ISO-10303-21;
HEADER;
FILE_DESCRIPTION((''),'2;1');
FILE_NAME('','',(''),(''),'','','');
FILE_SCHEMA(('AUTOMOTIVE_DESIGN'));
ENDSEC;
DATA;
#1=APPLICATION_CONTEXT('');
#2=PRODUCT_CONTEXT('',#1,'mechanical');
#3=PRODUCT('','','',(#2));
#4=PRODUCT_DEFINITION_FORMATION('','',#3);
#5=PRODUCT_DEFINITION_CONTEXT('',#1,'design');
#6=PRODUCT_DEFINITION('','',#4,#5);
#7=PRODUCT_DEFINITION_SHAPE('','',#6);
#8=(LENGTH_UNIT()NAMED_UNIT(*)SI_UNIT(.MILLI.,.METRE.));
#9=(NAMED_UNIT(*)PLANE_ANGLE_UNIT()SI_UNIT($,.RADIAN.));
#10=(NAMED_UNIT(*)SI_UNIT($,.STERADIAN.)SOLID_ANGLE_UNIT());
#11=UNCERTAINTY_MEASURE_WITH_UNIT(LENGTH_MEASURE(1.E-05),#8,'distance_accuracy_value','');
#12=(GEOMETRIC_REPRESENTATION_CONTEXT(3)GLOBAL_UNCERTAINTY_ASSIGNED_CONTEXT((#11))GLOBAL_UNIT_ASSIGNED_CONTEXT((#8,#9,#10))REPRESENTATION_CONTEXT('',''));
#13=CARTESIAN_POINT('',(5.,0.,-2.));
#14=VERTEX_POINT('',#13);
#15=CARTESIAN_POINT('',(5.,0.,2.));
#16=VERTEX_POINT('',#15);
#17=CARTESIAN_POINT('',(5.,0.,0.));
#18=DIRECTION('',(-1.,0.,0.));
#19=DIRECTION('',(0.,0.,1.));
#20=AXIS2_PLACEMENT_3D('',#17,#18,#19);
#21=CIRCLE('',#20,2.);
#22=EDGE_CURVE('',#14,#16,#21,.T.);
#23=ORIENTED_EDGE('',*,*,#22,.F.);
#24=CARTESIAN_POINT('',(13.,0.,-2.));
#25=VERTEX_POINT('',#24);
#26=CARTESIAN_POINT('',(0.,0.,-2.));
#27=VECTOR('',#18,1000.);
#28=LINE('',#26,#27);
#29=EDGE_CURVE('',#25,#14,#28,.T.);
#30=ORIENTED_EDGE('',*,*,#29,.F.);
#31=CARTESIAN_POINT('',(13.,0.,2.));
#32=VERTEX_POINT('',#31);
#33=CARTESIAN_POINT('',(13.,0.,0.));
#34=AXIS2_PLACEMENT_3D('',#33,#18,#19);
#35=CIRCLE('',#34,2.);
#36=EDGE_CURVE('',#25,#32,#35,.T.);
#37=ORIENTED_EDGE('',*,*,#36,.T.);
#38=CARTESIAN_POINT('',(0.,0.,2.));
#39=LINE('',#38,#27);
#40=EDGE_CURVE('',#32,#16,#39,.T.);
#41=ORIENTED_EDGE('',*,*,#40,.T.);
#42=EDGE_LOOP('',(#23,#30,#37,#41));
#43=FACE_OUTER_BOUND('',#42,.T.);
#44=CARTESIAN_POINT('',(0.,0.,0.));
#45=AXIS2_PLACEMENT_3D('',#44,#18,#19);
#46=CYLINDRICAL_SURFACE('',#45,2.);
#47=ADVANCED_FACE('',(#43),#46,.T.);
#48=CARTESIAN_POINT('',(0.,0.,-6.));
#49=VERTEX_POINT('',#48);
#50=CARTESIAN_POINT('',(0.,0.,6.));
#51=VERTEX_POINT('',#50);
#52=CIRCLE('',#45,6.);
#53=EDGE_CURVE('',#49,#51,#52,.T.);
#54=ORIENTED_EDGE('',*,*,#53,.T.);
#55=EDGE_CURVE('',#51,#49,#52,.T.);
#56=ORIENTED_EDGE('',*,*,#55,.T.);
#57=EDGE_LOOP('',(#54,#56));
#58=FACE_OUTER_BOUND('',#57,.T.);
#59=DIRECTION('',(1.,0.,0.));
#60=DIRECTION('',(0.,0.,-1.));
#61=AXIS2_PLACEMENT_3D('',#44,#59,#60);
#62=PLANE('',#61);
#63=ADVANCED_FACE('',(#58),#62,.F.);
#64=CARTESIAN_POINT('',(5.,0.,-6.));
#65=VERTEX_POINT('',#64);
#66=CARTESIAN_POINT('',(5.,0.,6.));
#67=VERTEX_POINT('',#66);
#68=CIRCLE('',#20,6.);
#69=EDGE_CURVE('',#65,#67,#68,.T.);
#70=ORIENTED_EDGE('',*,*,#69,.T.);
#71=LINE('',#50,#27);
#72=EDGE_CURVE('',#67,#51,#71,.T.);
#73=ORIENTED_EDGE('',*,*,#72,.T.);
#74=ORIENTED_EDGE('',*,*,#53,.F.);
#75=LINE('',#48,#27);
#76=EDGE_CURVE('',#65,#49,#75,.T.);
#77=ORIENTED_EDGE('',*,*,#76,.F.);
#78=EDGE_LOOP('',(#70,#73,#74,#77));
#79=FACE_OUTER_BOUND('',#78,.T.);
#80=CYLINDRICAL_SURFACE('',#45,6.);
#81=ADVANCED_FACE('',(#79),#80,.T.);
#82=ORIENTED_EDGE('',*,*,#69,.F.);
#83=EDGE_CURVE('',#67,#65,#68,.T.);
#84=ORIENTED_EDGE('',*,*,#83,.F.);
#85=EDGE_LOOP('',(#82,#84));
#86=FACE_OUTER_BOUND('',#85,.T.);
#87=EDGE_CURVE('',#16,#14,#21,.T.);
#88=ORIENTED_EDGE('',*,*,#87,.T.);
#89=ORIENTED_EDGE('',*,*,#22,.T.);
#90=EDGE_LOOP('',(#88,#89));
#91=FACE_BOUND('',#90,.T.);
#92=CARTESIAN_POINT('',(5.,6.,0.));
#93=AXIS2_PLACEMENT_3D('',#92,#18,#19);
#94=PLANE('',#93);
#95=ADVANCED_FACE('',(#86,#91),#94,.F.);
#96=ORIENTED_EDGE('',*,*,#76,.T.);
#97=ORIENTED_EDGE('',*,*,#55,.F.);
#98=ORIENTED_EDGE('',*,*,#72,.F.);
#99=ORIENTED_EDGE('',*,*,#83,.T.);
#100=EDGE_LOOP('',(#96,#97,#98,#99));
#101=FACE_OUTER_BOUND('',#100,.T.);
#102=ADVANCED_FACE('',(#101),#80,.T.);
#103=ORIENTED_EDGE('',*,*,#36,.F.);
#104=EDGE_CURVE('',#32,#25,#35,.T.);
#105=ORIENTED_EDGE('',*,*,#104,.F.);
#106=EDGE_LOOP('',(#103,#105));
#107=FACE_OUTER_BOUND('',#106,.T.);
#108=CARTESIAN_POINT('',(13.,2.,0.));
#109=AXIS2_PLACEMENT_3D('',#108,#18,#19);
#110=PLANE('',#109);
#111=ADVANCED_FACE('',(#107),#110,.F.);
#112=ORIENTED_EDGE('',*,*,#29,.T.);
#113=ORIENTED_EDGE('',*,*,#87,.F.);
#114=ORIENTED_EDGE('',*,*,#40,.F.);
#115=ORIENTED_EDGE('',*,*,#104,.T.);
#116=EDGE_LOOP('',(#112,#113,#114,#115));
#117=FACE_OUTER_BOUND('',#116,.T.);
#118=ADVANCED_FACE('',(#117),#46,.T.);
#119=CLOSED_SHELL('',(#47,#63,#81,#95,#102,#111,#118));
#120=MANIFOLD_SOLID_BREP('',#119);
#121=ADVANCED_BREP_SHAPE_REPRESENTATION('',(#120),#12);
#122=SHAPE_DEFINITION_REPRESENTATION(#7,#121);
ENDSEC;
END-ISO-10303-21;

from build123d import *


with BuildPart() as part:
    # Sketch1 → Revolve1 (revolve)
    with BuildSketch(Plane.XY, mode=Mode.PRIVATE) as revolve1_sk:
        Polygon((0, 0), (0, 6), (5, 6), (5, 2), (13, 2), (13, 0), align=None)
    revolve(revolve1_sk.sketch.rotate(Axis((0, 0, 0), (1, 0, 0)), 90), axis=Axis((0, 0, 0), (1, 0, 0)))


solid = part.part
